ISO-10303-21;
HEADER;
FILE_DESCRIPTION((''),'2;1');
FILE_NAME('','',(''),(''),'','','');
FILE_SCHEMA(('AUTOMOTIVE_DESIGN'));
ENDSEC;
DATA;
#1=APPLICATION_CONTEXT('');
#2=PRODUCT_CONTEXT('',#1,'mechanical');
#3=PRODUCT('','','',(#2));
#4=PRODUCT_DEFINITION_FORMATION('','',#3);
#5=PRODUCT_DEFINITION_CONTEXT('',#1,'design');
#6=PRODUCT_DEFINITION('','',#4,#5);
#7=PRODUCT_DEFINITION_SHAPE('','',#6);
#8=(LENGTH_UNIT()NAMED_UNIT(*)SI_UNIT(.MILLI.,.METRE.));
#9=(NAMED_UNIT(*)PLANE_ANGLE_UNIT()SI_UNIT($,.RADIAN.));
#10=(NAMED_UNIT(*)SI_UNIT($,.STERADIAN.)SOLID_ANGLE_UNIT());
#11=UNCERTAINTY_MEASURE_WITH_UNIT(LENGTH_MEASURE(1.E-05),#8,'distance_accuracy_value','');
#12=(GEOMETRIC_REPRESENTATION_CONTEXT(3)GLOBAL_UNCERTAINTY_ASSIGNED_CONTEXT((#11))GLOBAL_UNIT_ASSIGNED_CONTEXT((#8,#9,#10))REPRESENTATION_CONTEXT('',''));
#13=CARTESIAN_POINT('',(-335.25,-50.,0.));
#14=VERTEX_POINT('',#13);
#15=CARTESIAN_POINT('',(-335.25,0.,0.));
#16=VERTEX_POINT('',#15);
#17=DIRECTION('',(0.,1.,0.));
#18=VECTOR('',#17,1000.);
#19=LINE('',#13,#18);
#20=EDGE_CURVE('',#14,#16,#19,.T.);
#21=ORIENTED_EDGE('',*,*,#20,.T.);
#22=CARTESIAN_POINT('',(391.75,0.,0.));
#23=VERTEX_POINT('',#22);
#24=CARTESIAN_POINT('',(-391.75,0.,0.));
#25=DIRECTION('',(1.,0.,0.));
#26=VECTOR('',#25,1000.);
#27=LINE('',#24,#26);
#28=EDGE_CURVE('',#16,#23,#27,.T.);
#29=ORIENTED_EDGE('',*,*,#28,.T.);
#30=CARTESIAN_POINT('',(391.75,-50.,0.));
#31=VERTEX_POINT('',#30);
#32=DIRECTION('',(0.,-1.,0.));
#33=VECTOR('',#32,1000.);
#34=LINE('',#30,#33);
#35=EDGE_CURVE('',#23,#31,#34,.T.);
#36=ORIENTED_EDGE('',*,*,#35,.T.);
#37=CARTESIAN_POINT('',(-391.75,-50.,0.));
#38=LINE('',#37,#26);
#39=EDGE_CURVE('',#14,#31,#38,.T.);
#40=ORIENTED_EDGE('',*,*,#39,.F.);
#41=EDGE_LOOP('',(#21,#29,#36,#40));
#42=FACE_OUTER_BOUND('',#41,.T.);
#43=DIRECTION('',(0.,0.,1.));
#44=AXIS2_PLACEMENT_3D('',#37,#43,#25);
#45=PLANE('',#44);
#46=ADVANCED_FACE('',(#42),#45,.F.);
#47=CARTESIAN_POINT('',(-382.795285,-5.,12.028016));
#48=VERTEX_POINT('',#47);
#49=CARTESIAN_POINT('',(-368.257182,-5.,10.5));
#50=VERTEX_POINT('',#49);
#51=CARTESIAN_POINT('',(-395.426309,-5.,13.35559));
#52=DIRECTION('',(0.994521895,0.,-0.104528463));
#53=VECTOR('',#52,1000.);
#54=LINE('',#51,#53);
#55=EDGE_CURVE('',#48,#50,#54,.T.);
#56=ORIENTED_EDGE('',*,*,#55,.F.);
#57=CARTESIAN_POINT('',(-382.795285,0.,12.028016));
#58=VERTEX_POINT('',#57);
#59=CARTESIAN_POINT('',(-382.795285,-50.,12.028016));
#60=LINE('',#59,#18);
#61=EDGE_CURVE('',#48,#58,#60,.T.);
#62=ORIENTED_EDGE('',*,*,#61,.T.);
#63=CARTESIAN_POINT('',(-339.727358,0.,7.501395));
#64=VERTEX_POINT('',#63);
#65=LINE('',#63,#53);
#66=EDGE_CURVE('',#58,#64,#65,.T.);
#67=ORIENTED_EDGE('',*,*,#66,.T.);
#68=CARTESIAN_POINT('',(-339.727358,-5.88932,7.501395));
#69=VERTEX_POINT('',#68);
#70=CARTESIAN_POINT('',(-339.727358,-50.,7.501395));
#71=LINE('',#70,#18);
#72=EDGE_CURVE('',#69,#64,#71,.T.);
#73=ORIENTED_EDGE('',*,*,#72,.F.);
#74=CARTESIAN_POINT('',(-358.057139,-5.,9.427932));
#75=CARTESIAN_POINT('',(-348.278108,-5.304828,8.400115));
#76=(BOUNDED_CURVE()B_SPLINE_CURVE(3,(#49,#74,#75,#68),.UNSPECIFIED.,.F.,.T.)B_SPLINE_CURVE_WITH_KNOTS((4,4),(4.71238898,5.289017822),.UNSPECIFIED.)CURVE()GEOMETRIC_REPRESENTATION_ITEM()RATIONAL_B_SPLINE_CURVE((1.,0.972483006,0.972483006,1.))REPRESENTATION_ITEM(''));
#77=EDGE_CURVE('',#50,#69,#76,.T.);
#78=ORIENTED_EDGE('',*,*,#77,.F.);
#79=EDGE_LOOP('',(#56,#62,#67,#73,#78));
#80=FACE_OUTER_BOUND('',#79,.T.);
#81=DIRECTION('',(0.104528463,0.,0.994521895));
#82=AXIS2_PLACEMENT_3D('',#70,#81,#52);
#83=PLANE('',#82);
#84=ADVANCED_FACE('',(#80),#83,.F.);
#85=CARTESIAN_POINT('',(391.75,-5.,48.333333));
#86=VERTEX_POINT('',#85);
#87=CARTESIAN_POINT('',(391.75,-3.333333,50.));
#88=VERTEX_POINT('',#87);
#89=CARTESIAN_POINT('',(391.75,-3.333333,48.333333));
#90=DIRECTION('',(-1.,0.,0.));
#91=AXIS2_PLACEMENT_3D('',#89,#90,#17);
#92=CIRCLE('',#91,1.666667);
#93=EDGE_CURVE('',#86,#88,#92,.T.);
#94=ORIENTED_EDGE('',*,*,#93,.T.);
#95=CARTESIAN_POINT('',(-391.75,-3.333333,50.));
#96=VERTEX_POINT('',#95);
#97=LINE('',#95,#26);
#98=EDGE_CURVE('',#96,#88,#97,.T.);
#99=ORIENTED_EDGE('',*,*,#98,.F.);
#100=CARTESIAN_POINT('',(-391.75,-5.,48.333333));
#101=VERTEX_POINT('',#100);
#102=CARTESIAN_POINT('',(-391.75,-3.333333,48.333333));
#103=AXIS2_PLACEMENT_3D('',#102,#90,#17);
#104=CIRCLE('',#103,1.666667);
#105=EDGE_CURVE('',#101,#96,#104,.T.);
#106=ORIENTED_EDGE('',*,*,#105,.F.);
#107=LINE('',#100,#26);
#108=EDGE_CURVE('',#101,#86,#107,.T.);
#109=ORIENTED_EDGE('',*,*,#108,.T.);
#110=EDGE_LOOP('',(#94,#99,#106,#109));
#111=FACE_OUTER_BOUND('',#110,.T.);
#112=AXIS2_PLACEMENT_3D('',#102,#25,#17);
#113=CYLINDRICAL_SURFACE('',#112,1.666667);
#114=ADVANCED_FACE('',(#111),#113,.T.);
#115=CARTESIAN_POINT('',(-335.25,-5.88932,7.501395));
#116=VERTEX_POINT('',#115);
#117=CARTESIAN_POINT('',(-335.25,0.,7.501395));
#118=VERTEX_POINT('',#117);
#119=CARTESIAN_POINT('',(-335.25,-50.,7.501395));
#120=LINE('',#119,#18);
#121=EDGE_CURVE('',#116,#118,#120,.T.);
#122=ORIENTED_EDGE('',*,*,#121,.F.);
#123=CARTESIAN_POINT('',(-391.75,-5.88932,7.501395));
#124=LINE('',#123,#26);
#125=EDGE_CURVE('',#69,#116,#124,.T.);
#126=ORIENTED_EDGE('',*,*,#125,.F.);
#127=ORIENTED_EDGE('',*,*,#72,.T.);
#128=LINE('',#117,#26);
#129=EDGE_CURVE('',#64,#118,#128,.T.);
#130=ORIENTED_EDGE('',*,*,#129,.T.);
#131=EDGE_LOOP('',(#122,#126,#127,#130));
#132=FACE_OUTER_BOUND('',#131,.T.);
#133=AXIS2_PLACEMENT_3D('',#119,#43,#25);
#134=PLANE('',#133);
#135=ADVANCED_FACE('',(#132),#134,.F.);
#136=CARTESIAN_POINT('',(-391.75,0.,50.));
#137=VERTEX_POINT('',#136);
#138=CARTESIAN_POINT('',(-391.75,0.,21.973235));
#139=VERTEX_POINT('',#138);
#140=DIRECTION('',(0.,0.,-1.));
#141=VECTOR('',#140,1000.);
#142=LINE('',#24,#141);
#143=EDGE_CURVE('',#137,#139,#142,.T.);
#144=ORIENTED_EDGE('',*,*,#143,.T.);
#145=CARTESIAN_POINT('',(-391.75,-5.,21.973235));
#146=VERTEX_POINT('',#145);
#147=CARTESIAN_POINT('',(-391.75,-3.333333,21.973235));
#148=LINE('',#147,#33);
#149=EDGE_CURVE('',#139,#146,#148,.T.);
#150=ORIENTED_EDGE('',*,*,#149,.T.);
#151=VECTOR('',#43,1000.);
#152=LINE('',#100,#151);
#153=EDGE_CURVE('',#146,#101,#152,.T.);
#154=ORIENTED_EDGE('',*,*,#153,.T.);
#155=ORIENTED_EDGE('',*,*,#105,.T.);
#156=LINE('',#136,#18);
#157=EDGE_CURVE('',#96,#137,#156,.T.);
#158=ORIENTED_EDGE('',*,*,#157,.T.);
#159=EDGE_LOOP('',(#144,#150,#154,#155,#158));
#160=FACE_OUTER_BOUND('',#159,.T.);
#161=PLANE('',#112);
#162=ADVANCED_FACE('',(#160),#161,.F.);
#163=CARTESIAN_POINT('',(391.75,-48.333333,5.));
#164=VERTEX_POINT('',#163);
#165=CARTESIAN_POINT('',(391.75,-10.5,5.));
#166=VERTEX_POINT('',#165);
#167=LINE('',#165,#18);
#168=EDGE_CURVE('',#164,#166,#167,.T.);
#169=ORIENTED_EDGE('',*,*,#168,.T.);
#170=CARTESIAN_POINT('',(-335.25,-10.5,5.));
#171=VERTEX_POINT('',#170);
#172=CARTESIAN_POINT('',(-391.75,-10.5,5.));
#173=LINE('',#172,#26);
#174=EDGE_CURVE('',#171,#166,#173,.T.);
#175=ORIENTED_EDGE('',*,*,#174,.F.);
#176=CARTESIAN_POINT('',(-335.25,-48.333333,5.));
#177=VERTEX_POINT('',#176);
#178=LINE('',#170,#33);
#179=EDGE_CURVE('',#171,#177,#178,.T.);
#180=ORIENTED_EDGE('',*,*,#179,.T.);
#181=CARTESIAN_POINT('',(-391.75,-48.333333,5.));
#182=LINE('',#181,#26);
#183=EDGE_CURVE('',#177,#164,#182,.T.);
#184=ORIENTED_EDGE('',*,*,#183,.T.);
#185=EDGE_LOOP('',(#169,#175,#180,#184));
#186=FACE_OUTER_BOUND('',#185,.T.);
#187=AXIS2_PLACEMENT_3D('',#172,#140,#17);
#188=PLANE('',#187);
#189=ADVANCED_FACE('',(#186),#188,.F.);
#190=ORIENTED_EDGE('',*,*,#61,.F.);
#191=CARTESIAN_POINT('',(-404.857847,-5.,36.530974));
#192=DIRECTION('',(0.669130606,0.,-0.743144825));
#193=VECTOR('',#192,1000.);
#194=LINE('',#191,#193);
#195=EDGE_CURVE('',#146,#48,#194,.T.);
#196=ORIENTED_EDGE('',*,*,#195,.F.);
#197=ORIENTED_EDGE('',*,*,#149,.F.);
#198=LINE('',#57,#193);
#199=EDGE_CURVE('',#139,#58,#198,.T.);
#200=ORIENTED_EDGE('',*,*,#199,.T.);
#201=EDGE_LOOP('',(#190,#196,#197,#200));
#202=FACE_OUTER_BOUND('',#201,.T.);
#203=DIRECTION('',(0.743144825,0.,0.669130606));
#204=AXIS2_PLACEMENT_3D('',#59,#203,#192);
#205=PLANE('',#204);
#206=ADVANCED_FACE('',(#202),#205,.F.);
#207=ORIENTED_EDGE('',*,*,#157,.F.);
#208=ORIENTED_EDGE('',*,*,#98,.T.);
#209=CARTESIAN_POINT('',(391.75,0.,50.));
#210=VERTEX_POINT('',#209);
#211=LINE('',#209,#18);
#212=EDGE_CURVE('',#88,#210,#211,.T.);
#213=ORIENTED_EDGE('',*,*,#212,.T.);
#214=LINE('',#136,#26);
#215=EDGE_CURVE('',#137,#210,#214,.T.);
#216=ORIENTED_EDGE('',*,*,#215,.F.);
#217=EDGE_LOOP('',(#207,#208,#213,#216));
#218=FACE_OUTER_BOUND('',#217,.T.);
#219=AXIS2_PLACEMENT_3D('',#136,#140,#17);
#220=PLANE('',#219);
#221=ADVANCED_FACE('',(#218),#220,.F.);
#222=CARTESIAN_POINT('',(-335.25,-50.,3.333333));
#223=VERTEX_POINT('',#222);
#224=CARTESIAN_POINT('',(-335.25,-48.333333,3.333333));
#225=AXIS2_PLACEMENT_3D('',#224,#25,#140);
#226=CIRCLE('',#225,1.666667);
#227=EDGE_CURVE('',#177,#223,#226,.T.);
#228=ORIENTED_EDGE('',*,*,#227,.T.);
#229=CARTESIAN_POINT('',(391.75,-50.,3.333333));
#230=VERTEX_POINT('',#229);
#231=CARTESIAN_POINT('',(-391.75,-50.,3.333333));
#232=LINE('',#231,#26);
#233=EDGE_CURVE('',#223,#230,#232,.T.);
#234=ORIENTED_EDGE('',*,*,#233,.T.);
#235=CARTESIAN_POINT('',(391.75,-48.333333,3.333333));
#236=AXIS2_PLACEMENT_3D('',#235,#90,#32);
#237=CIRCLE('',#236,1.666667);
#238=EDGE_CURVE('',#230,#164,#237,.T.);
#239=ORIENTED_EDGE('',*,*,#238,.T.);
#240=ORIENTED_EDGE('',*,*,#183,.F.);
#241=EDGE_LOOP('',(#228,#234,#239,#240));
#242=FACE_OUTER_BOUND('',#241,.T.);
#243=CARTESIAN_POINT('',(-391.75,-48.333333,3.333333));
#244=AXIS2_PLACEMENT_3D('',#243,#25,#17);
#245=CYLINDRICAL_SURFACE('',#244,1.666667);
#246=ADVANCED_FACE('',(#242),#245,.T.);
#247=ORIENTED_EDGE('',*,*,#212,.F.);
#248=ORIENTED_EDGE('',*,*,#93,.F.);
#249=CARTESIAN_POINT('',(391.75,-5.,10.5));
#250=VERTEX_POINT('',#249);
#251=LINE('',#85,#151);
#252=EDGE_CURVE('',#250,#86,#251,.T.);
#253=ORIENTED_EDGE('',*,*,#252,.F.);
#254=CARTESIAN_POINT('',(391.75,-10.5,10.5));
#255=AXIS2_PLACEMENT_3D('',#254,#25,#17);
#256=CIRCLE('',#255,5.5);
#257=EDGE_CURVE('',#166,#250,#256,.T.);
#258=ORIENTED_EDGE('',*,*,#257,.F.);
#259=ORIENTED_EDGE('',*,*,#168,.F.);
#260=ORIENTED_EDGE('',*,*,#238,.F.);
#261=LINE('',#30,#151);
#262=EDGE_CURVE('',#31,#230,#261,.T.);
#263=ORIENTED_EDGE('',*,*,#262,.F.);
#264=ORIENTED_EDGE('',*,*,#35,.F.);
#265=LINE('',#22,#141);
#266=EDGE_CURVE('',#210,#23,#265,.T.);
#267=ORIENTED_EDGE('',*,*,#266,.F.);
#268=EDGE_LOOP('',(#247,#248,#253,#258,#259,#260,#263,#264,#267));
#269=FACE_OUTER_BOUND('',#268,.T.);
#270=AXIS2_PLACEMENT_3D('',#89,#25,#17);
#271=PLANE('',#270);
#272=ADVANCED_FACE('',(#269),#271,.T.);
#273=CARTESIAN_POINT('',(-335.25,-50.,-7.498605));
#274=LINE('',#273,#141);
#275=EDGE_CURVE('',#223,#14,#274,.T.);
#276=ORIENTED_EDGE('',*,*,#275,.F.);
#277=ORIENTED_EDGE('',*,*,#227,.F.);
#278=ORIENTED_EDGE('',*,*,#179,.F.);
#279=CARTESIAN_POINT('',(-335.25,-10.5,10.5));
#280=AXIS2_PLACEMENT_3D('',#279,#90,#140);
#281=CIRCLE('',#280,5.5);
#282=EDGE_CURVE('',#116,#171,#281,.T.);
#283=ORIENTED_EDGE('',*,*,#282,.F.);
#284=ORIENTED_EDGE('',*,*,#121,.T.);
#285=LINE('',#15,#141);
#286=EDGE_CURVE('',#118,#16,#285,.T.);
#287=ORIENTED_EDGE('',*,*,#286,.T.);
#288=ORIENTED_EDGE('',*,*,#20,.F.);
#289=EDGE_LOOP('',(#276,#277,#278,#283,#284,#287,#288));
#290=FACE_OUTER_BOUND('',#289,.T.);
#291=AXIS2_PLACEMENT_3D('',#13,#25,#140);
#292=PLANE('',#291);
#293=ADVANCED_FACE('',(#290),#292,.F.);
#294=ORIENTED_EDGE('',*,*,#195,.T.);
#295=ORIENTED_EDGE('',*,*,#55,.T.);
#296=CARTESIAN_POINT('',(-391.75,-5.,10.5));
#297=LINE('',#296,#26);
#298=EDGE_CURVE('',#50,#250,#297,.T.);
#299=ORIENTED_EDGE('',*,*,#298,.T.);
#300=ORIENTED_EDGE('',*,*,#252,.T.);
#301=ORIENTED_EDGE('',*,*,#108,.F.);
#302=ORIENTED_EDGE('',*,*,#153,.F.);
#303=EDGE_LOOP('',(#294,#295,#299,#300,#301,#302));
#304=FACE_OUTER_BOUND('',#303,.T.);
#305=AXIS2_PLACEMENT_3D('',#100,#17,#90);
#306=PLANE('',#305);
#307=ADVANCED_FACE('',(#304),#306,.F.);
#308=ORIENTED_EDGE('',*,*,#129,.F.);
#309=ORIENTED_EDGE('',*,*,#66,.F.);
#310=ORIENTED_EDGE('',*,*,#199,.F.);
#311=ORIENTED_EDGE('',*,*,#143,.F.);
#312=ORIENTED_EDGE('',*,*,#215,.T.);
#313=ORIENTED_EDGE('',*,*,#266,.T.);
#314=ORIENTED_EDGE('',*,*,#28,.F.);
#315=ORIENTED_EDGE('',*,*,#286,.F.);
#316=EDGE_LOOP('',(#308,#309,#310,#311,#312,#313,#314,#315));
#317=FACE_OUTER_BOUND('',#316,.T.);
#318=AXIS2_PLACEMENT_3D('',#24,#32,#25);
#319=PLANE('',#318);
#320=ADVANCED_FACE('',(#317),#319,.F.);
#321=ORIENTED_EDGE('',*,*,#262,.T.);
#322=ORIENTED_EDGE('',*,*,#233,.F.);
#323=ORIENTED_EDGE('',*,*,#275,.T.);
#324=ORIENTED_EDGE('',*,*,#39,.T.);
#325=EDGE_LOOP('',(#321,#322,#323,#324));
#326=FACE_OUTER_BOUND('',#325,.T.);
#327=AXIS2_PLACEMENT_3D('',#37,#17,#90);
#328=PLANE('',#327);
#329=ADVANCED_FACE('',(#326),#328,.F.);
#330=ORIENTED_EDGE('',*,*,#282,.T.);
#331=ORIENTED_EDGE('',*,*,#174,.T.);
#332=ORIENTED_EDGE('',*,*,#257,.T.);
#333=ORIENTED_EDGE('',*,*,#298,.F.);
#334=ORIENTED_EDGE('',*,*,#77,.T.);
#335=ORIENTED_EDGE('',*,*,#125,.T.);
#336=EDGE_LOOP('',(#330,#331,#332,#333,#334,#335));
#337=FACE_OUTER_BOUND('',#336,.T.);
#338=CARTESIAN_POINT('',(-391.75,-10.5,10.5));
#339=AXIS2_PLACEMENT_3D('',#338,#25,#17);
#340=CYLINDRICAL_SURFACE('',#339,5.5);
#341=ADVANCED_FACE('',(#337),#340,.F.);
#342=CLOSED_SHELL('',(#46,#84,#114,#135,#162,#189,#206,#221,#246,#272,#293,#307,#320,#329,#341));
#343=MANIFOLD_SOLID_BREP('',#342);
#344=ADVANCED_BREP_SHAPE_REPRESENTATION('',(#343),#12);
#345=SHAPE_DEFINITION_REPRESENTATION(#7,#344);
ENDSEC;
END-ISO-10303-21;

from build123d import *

# Parameters (mm, degrees)
GBT706_2008_050_5_1_DEPTH = 783.5
CUT_EXTRUDE_1_DEPTH       = 399.080472392


with BuildPart() as part:
    # Sketch1 → Gbt706-2008 热轧等边角钢 050×5(1) (new body)
    with BuildSketch(Plane(origin=(391.75, 0, 0), x_dir=(0, -1, 0), z_dir=(-1, 0, 0))):
        with BuildLine():
            Line((0, 0), (0, 50))
            Line((0, 50), (3.333333333, 50))
            ThreePointArc((3.333333333, 50), (4.511844635, 49.511844635), (5, 48.333333333))
            Line((5, 48.333333333), (5, 10.5))
            ThreePointArc((5, 10.5), (6.610912703, 6.610912703), (10.5, 5))
            Line((10.5, 5), (48.333333333, 5))
            ThreePointArc((48.333333333, 5), (49.511844635, 4.511844635), (50, 3.333333333))
            Line((50, 3.333333333), (50, 0))
            Line((50, 0), (0, 0))
        make_face()
    extrude(amount=GBT706_2008_050_5_1_DEPTH)

    # 草图2 → 切除-拉伸1 (cut, through all)
    with BuildSketch(Plane(origin=(0, 0, 0), x_dir=(1, 0, 0), z_dir=(0, 1, 0))):
        Polygon((-335.25, 0), (-335.25, -7.501394609), (-339.727357684, -7.501394609), (-382.795284633, -12.028016136), (-391.75, -21.973235089), (-391.75, -52.501394609), (-406.75, -52.501394609), (-406.75, 7.498605391), (-335.25, 7.498605391), align=None)
    extrude(amount=-CUT_EXTRUDE_1_DEPTH, mode=Mode.SUBTRACT)


solid = part.part
